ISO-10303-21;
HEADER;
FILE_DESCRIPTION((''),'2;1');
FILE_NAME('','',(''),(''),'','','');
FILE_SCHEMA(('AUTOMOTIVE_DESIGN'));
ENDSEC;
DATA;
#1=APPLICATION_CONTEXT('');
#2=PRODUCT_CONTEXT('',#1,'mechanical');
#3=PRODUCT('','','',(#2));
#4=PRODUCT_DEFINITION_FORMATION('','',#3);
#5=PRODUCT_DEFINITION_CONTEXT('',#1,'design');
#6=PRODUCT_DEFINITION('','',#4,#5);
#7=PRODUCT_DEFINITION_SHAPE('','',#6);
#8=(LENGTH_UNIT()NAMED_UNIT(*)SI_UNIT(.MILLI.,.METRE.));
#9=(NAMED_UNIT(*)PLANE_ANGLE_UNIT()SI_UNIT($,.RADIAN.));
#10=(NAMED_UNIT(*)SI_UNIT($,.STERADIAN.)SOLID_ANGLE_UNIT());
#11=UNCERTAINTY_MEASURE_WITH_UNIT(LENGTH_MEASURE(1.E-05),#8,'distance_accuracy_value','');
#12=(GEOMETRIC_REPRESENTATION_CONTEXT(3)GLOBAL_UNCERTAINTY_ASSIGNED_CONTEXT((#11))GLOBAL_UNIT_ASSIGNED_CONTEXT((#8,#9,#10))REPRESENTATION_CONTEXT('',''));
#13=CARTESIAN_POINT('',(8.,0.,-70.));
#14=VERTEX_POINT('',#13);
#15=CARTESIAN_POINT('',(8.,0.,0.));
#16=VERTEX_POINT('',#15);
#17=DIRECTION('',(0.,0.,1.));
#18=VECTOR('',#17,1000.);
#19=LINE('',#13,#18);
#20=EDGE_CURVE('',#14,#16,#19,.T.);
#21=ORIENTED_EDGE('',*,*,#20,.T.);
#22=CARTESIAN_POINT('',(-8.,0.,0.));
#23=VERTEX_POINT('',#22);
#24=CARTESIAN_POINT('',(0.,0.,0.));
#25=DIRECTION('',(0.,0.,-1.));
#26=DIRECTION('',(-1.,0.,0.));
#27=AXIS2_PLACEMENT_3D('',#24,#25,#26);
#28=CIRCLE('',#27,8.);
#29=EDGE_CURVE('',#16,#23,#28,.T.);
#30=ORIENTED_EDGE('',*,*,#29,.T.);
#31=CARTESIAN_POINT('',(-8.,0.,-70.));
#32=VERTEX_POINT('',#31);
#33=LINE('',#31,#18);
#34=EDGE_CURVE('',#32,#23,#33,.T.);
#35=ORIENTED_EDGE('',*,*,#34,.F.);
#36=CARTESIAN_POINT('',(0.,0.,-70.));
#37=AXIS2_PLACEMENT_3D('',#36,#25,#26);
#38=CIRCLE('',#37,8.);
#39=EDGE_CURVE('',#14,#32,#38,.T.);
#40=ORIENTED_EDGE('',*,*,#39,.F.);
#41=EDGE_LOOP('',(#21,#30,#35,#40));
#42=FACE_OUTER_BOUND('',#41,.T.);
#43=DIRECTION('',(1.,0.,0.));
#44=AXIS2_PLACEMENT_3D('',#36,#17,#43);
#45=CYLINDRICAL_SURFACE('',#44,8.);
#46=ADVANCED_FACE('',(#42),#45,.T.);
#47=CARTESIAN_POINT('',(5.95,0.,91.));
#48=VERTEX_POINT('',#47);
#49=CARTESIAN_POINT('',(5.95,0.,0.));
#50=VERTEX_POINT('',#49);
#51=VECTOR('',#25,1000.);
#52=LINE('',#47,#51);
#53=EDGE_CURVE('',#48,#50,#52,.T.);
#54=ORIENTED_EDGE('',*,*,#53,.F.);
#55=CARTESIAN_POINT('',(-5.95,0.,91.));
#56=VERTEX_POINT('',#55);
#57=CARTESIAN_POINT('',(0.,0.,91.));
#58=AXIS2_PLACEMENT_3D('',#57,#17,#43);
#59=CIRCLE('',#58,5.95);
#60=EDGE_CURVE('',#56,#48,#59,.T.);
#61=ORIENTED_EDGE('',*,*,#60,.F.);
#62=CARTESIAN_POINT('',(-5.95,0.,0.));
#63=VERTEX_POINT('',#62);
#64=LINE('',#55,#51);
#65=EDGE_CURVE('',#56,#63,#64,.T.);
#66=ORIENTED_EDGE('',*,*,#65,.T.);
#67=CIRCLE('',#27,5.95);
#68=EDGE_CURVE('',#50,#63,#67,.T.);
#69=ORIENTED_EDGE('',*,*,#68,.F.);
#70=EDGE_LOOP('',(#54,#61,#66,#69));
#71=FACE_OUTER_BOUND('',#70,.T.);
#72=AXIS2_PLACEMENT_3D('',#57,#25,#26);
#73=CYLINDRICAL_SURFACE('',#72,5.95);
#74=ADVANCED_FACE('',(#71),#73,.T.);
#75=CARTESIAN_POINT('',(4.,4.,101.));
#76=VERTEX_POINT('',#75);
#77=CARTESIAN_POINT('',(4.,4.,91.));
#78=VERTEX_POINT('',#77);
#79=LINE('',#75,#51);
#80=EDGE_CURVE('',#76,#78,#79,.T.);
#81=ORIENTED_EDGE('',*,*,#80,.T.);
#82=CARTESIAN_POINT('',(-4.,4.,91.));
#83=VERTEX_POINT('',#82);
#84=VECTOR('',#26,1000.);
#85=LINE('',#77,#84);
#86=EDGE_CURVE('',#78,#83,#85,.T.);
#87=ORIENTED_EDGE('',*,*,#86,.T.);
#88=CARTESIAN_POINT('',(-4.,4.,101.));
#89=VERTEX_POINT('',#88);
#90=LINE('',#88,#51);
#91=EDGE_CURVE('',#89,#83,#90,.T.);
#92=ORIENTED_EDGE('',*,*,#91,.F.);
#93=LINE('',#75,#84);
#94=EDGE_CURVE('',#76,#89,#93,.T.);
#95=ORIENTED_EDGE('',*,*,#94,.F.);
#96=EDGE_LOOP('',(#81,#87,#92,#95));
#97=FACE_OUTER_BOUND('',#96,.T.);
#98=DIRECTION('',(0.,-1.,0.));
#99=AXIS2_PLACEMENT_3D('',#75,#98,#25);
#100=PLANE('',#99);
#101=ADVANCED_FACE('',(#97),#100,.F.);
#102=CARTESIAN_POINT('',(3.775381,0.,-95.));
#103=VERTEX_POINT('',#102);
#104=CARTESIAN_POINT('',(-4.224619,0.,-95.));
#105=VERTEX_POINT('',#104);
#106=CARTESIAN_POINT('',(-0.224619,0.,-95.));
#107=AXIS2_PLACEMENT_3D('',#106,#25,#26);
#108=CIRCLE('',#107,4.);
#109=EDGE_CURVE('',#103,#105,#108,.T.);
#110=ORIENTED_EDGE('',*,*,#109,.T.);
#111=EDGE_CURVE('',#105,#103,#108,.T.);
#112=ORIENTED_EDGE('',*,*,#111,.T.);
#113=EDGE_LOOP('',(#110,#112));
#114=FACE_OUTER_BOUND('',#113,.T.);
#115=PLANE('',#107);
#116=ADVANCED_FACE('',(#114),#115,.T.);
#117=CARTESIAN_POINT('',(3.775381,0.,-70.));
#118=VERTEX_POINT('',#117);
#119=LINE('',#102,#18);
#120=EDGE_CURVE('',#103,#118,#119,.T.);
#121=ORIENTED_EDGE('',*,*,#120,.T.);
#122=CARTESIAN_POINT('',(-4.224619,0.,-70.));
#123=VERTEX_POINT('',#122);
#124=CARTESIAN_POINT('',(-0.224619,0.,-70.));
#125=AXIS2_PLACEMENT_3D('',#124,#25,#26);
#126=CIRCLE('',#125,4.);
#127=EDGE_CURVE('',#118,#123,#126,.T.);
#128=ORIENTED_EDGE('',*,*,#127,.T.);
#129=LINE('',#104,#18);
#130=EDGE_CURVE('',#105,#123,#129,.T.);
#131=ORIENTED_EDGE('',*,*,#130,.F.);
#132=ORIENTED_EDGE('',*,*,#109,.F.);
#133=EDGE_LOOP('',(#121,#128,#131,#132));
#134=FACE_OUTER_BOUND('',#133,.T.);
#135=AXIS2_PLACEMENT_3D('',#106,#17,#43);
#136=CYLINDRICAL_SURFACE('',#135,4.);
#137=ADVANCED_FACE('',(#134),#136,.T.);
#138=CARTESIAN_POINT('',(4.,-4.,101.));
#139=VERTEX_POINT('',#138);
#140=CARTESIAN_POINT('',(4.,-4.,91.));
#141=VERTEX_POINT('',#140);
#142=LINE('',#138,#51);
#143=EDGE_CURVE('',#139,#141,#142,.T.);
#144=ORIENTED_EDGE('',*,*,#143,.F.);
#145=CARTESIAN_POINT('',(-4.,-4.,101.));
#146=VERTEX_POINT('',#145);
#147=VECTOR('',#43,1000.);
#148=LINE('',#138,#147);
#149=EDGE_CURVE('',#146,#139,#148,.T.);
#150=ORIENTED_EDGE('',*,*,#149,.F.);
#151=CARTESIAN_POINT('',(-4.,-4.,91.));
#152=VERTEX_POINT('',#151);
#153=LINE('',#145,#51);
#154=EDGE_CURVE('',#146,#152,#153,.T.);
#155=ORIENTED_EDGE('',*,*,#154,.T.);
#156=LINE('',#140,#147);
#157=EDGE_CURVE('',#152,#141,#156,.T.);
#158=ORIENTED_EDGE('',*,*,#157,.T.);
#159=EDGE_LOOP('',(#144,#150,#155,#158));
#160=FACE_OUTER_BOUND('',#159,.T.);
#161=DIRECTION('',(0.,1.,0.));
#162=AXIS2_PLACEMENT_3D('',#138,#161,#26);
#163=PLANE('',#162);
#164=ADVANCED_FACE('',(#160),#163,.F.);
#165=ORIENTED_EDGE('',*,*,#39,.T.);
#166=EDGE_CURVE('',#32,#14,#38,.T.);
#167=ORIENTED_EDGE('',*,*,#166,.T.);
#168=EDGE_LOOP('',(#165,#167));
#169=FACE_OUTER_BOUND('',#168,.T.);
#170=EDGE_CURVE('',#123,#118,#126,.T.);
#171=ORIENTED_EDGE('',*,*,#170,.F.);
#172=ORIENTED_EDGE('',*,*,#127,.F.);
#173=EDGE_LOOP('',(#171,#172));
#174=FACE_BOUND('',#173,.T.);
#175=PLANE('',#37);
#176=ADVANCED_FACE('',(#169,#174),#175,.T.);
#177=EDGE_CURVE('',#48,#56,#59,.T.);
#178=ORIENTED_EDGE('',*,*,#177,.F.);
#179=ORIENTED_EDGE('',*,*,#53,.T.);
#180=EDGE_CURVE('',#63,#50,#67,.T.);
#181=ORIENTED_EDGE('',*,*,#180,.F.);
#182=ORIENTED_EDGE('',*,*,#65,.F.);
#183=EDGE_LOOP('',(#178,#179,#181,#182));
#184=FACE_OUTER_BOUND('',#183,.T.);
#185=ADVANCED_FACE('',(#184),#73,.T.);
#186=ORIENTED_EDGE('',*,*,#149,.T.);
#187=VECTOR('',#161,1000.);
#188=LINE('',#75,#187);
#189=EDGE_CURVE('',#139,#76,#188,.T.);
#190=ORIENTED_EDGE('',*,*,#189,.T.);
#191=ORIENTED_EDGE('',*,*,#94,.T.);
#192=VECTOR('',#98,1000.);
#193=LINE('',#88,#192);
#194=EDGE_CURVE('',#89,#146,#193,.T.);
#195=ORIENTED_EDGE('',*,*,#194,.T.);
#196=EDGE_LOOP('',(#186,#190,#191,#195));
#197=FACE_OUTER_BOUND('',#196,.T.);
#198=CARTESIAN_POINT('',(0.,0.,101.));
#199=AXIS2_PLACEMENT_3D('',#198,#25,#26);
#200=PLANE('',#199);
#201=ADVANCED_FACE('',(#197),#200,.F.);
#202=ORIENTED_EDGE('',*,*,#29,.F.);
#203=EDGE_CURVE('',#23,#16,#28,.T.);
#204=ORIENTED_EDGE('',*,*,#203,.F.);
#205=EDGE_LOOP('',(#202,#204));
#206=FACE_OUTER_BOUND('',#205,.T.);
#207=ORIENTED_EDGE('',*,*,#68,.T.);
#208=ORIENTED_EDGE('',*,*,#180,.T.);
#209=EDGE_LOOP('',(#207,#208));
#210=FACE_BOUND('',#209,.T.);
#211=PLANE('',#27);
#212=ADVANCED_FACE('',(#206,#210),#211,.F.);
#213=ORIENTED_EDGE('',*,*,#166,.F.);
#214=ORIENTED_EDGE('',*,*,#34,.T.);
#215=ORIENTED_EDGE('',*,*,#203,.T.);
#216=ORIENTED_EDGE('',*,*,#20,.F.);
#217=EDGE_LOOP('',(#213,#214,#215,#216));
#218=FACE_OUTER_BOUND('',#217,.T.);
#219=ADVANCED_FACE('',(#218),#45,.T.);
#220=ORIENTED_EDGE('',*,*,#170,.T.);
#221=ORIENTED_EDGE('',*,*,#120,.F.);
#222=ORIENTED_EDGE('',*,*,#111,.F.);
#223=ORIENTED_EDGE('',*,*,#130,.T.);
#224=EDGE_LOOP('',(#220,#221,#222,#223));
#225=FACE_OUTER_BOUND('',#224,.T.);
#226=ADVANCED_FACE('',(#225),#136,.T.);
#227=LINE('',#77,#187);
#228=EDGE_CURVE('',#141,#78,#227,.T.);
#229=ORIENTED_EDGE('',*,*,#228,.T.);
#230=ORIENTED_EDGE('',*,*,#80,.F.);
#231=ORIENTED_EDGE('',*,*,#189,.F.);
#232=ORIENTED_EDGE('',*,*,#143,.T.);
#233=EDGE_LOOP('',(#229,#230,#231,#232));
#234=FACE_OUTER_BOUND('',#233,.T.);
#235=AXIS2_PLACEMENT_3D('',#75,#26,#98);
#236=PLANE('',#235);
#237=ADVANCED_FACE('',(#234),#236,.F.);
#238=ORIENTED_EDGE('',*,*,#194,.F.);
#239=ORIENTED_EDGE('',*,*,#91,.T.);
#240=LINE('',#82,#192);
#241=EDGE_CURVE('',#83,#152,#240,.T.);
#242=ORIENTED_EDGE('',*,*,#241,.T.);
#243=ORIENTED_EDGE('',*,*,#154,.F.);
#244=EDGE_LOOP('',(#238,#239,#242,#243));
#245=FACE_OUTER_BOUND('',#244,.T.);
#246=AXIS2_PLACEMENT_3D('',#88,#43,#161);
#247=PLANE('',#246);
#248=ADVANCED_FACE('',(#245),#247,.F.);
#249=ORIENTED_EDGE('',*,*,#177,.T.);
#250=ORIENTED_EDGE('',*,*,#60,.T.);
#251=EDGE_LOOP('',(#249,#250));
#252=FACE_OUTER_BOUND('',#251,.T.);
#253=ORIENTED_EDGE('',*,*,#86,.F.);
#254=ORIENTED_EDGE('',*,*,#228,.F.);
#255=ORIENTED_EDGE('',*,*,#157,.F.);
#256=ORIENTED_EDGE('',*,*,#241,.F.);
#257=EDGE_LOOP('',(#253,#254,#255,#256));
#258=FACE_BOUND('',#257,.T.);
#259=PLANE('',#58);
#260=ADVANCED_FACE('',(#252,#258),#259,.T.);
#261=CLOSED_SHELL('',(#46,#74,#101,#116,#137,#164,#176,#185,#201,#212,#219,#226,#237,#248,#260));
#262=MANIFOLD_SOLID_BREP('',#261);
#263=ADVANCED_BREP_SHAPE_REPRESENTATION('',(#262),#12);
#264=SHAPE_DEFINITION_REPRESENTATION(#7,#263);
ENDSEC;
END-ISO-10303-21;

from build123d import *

# Parameters (mm, degrees)
SKETCH_1_R      = 5.95
EXTRUDE_1_DEPTH = 91
SKETCH_2_W      = 8
SKETCH_2_H      = 8
EXTRUDE_2_DEPTH = 10
SKETCH_3_R      = 8
EXTRUDE_3_DEPTH = 70
SKETCH_4_R      = 4
EXTRUDE_4_DEPTH = 25


with BuildPart() as part:
    # 草图1 → 凸台-拉伸1 (new body)
    with BuildSketch(Plane.XY):
        Circle(SKETCH_1_R)
    extrude(amount=EXTRUDE_1_DEPTH)

    # 草图2 → 凸台-拉伸2 (add)
    with BuildSketch(Plane.XY.offset(91)):
        Rectangle(SKETCH_2_W, SKETCH_2_H)
    extrude(amount=EXTRUDE_2_DEPTH)

    # 草图3 → 凸台-拉伸3 (add)
    with BuildSketch(Plane(origin=(0, 0, 0), x_dir=(-1, 0, 0), z_dir=(0, 0, -1))):
        Circle(SKETCH_3_R)
    extrude(amount=EXTRUDE_3_DEPTH)

    # 草图4 → 凸台-拉伸4 (add)
    with BuildSketch(Plane(origin=(0, 0, -70), x_dir=(-1, 0, 0), z_dir=(0, 0, -1))):
        with Locations((0.224619263, 0)):
            Circle(SKETCH_4_R)
    extrude(amount=EXTRUDE_4_DEPTH)


solid = part.part
